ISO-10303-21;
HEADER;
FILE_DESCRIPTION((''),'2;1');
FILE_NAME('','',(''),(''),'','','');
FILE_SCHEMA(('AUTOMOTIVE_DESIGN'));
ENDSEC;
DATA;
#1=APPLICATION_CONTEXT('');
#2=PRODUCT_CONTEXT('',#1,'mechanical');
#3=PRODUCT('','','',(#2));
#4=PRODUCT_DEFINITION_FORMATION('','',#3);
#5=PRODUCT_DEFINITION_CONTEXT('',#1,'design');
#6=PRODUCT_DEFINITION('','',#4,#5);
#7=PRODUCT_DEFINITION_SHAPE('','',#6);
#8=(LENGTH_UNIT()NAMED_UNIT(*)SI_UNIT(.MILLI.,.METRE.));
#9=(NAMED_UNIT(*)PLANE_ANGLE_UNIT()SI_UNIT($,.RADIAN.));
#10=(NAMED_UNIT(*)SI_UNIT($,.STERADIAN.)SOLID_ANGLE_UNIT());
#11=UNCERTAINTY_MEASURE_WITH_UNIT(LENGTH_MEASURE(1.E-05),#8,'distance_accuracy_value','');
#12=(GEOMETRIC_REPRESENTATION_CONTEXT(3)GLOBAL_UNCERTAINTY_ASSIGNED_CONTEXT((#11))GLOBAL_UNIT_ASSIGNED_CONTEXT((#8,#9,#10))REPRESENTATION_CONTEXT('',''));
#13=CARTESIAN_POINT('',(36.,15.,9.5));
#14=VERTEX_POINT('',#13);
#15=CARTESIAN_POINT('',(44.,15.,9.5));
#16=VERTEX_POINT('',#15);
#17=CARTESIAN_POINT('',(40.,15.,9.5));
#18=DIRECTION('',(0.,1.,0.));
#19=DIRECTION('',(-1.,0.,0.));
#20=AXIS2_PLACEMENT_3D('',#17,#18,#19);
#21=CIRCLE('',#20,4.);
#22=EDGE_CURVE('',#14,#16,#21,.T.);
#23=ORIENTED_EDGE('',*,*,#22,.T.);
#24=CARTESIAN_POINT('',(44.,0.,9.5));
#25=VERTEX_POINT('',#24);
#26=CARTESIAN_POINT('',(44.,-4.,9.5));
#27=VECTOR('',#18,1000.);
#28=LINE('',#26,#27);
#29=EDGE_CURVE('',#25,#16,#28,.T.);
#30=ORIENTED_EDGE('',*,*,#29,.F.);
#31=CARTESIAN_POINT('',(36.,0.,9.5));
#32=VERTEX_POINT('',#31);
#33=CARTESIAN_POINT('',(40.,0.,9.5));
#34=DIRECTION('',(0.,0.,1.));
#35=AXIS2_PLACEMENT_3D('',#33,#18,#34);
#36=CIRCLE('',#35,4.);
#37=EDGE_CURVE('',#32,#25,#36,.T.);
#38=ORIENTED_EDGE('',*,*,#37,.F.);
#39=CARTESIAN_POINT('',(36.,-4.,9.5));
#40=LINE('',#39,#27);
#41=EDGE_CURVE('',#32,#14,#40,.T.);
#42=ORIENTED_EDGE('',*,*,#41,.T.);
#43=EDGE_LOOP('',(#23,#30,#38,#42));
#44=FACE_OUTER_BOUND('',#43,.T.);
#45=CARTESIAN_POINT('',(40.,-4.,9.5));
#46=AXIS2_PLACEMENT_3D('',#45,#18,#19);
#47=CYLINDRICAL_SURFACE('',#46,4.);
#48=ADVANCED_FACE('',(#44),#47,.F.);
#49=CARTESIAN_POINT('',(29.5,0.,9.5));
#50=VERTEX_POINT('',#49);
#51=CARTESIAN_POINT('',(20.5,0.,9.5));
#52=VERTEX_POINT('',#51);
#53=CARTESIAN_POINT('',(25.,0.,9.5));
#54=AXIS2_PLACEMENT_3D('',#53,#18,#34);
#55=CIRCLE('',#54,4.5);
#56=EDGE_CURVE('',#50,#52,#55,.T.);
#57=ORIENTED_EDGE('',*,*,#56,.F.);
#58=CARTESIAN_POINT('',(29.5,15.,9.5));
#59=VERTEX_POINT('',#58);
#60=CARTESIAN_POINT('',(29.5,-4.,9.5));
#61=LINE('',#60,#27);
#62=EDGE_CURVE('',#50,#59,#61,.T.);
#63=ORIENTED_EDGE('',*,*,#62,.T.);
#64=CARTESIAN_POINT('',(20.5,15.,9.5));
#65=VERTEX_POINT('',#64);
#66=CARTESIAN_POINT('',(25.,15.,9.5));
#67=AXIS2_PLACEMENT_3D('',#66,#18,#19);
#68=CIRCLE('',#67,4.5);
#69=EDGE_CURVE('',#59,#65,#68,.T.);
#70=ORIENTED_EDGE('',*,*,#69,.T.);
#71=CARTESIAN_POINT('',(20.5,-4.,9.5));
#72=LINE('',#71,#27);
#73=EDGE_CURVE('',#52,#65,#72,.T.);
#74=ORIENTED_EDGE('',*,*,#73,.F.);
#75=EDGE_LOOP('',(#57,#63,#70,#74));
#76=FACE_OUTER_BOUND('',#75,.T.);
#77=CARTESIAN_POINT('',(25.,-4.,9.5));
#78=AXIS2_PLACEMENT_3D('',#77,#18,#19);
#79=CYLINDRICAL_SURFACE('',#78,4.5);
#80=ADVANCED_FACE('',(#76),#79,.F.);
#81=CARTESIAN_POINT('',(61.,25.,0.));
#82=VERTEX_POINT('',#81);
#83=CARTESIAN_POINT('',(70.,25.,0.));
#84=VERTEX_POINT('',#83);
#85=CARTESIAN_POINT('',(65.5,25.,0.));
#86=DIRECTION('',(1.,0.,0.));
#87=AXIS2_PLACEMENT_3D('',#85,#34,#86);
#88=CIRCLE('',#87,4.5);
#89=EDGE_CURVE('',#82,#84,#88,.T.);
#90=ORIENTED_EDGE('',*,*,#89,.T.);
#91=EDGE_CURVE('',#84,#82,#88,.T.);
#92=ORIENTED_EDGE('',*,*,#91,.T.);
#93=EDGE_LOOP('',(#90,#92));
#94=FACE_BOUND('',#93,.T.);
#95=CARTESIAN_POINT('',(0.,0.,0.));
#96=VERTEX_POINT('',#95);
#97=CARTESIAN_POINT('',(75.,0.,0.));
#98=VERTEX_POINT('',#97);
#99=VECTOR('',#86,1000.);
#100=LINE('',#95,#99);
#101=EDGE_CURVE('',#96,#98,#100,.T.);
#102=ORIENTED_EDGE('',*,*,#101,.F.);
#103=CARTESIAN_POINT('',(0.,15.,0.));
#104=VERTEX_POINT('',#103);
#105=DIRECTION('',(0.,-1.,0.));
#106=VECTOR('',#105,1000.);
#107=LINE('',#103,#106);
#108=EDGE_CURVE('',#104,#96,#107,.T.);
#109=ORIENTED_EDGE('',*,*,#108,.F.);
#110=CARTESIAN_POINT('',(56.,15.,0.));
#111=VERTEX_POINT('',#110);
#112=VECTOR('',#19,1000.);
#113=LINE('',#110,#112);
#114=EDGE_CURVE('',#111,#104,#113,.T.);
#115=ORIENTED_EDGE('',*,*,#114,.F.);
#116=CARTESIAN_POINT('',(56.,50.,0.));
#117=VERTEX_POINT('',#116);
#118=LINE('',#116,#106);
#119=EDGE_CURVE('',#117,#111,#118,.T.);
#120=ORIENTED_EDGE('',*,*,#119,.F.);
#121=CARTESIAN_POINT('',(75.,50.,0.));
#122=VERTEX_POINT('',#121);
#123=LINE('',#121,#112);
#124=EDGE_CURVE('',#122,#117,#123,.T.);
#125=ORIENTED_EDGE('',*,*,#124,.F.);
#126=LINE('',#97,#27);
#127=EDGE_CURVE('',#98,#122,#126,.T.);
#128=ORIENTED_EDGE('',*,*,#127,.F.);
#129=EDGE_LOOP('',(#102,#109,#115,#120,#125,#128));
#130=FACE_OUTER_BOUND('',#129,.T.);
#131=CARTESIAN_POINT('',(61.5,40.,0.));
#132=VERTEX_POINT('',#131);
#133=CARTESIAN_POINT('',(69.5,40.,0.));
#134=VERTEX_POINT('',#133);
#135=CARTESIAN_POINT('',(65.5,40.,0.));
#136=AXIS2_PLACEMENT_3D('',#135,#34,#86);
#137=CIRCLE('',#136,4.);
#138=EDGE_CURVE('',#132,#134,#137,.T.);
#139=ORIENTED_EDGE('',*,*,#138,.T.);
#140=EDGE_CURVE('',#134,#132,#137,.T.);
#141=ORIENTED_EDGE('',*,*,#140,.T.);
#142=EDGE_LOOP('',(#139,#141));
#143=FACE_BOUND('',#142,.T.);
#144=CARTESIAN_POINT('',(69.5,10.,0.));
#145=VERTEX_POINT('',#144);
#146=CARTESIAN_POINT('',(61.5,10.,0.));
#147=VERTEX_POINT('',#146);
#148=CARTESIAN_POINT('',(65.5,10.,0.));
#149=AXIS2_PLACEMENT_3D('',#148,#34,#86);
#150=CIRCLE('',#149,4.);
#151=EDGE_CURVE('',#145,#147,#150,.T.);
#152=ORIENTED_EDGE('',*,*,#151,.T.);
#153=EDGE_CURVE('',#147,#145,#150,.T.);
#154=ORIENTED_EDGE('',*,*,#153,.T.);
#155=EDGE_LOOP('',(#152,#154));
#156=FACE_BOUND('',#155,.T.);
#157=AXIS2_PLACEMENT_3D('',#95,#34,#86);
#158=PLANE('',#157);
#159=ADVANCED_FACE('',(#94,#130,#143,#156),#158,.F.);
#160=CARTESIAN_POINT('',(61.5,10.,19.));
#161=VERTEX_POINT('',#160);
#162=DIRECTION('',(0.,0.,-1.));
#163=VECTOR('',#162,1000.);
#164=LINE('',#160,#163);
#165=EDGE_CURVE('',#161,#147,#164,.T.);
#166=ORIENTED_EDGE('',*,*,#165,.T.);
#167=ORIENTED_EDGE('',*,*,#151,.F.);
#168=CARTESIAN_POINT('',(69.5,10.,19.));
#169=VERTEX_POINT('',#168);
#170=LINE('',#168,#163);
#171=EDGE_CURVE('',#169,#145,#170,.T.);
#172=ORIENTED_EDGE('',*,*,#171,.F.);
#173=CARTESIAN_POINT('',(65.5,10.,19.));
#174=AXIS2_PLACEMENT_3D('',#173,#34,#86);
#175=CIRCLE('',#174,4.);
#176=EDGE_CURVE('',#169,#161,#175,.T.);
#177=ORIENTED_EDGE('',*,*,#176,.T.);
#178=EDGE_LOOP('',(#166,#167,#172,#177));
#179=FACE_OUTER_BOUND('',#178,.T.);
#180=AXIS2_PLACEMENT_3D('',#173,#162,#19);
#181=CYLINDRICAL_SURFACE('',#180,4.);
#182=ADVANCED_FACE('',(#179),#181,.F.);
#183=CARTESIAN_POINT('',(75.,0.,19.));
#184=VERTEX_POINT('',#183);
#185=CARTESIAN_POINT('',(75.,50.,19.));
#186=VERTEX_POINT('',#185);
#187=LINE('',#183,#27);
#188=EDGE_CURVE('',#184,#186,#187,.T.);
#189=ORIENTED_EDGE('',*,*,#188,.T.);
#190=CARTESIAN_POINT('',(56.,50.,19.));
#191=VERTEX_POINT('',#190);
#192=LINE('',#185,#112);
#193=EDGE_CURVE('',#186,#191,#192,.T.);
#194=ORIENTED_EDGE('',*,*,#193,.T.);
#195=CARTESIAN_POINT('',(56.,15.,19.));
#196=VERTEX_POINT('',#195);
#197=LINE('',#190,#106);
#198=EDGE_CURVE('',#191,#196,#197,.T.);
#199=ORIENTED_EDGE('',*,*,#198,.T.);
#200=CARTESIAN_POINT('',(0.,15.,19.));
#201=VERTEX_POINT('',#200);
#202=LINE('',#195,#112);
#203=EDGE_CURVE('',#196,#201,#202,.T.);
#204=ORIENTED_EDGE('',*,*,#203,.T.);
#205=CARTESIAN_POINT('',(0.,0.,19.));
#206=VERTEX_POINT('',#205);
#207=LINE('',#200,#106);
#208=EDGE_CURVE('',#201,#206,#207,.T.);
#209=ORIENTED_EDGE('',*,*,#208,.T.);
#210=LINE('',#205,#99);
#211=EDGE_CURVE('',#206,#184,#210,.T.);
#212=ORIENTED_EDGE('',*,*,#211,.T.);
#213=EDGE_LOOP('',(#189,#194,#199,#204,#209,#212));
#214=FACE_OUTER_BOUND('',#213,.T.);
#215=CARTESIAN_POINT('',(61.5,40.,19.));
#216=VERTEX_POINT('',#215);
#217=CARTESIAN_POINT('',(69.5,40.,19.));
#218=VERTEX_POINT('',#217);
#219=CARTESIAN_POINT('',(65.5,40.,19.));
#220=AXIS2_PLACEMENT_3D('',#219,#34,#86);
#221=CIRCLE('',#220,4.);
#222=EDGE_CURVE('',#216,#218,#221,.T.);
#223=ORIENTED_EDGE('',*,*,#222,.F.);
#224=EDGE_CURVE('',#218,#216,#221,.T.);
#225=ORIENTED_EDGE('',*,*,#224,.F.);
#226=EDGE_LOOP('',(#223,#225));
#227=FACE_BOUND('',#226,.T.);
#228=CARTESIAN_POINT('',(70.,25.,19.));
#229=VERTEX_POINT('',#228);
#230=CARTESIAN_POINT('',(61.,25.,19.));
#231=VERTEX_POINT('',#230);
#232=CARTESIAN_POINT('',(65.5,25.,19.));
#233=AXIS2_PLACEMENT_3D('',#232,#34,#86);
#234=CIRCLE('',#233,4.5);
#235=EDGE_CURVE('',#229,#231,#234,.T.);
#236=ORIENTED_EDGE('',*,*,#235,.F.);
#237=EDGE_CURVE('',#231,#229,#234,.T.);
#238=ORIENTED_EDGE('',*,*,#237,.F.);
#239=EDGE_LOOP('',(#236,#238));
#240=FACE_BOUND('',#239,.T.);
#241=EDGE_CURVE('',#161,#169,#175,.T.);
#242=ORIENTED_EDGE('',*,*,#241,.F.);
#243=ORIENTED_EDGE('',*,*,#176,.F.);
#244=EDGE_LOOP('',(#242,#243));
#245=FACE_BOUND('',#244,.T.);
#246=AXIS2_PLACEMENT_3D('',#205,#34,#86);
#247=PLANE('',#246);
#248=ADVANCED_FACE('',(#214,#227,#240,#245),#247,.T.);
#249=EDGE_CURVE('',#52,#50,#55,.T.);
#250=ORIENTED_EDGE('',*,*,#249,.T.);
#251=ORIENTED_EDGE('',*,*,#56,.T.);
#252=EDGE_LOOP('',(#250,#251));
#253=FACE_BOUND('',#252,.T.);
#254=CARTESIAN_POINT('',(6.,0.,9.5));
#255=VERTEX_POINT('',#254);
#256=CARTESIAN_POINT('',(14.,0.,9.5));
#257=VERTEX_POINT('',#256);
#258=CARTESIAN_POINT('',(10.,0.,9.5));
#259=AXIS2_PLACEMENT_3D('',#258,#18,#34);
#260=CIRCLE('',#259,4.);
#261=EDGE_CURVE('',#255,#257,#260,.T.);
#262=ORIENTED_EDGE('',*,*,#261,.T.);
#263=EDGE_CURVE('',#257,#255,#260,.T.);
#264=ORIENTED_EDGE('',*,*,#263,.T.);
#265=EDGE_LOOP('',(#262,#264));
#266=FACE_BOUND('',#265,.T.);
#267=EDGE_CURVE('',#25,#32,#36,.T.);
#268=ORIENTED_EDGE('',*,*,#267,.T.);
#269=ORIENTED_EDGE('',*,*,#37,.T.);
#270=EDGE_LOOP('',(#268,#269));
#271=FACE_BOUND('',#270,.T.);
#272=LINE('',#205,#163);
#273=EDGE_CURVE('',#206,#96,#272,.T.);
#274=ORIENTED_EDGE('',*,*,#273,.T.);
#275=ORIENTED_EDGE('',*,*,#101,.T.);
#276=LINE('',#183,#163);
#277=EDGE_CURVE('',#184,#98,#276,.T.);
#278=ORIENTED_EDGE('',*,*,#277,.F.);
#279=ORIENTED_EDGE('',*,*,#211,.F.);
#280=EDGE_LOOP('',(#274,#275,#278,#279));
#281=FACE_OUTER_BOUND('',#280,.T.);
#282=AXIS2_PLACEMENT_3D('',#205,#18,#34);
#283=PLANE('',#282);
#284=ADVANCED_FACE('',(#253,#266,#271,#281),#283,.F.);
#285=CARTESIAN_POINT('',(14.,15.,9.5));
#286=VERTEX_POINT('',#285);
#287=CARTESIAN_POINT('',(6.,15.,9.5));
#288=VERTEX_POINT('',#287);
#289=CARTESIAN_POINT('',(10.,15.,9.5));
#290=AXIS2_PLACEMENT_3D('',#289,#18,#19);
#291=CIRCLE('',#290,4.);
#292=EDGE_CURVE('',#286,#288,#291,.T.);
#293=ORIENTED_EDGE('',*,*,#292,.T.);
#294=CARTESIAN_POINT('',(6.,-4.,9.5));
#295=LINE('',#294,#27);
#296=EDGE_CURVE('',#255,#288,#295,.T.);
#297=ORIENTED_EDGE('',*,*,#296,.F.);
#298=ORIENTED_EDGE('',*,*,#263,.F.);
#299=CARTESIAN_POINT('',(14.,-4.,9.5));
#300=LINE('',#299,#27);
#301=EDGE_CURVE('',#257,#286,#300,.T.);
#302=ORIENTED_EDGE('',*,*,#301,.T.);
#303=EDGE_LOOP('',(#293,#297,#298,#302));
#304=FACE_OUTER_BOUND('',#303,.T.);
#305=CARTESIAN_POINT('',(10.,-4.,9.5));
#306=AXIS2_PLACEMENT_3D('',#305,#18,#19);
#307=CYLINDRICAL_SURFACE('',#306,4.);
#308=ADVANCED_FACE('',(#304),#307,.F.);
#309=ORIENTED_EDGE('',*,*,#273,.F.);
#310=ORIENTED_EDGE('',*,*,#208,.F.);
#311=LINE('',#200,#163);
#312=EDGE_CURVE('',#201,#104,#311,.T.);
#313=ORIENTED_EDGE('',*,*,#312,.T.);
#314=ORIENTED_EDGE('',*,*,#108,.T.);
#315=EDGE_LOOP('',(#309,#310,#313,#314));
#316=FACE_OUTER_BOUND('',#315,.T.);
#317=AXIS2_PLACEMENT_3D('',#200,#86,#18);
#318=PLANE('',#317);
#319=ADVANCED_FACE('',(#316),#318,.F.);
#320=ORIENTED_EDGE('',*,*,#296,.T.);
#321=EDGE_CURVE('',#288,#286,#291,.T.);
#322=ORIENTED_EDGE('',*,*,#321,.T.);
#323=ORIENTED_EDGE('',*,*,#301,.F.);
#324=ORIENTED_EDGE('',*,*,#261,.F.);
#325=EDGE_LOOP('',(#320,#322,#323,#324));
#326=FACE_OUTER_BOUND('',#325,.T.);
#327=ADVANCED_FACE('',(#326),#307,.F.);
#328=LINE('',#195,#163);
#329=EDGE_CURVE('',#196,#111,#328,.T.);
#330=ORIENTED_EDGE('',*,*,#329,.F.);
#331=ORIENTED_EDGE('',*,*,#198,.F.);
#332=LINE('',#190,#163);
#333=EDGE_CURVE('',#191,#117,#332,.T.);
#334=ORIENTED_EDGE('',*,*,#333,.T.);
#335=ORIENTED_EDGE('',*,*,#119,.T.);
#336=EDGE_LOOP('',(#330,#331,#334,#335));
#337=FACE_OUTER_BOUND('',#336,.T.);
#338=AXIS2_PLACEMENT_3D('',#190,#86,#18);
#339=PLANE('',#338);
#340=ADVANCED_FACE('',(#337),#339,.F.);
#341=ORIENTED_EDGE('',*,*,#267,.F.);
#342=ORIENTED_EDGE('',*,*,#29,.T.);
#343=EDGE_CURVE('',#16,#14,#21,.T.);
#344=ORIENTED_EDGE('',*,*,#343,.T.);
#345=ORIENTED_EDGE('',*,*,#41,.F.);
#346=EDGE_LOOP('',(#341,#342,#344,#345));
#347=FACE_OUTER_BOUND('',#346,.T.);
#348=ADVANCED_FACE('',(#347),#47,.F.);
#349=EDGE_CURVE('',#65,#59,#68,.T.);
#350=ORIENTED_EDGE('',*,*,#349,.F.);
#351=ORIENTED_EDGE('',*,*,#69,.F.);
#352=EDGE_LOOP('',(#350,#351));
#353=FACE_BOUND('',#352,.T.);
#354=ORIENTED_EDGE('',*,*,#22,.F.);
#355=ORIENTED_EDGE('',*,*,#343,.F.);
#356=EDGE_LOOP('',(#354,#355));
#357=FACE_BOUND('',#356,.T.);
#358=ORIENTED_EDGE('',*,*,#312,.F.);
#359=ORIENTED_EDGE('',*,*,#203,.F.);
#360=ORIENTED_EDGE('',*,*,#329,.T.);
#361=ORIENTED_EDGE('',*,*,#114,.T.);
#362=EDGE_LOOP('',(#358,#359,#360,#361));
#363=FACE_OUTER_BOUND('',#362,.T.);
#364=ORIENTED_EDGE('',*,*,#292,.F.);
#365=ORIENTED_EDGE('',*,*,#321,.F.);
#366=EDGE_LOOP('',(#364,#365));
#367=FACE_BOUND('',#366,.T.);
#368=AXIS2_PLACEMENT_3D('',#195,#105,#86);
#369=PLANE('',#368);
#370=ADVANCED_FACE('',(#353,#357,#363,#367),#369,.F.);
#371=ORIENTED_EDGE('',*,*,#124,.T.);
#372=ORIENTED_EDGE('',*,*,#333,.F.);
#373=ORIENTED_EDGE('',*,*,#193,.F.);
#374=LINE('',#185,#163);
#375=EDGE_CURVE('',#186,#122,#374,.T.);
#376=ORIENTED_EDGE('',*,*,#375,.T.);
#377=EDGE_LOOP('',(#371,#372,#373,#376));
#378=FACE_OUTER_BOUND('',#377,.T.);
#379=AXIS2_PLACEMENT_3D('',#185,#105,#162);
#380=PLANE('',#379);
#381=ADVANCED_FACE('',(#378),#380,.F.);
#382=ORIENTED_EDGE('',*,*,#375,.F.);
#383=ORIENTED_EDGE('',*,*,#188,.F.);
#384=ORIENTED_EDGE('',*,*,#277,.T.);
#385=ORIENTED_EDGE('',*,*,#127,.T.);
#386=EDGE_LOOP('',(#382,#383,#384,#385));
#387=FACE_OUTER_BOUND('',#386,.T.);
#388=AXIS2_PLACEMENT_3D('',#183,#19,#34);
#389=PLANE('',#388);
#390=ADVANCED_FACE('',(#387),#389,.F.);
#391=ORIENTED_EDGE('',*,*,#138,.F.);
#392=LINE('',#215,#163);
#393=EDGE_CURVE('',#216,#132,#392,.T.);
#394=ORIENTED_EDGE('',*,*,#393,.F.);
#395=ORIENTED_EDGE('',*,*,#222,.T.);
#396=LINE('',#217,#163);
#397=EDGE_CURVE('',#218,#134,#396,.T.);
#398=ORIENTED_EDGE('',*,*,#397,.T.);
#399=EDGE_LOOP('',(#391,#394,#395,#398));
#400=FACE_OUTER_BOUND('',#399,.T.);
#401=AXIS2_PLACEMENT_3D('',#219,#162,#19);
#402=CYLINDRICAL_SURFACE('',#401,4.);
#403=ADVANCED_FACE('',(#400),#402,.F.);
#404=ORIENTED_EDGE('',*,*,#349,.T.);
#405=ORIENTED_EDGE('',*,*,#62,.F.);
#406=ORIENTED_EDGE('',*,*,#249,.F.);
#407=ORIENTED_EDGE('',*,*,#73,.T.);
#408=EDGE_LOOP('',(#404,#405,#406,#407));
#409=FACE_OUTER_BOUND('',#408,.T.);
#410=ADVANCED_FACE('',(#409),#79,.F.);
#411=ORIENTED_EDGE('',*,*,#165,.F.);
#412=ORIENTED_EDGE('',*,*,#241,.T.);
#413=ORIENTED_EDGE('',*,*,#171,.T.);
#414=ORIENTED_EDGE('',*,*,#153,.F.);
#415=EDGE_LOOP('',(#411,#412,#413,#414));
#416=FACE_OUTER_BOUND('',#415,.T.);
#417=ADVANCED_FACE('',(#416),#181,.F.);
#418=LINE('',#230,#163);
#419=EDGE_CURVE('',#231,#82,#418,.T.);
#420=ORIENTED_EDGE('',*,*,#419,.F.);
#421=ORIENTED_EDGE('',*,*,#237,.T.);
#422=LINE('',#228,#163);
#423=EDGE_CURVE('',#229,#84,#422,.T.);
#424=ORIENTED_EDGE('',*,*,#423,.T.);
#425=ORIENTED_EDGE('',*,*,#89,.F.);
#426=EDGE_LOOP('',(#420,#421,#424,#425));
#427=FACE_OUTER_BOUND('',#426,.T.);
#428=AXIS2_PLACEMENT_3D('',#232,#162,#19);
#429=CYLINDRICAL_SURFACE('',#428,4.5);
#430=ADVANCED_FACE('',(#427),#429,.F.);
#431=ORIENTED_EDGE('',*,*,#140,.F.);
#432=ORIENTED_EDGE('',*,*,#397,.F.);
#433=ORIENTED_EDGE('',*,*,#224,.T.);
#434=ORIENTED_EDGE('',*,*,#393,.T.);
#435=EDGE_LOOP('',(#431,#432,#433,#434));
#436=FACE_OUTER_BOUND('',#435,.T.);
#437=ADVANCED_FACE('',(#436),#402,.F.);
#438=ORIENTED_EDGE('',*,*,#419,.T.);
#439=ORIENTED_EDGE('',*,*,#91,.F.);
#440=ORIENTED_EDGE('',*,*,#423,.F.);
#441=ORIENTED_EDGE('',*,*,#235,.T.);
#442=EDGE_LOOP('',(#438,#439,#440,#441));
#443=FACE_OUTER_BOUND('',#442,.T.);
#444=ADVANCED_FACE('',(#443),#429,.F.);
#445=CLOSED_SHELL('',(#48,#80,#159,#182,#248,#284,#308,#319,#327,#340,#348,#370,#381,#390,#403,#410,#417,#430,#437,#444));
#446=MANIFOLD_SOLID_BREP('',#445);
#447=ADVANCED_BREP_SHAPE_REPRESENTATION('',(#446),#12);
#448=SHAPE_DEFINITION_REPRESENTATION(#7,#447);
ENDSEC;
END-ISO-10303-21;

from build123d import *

# Parameters (mm, degrees)
SKETCH1_R           = 4
SKETCH1_R_2         = 4.5
BOSS_EXTRUDE1_DEPTH = 19
SKETCH2_R           = 4
SKETCH2_R_2         = 4.5
CUT_EXTRUDE1_DEPTH  = 19


with BuildPart() as part:
    # Sketch1 → Boss-Extrude1 (new body)
    with BuildSketch(Plane.XY):
        Polygon((0, 0), (75, 0), (75, 50), (56, 50), (56, 15), (0, 15), align=None)
        with Locations((65.5, 10)):
            Circle(SKETCH1_R, mode=Mode.SUBTRACT)
        with Locations((65.5, 25)):
            Circle(SKETCH1_R_2, mode=Mode.SUBTRACT)
        with Locations((65.5, 40)):
            Circle(SKETCH1_R, mode=Mode.SUBTRACT)
    extrude(amount=BOSS_EXTRUDE1_DEPTH)

    # Sketch2 → Cut-Extrude1 (cut)
    with BuildSketch(Plane(origin=(0, 15, 0), x_dir=(1, 0, 0), z_dir=(0, 1, 0))):
        with Locations(Location((10, -9.5, 0), (0, 0, 180))):
            Circle(SKETCH2_R)
        with Locations(Location((25, -9.5, 0), (0, 0, 180))):
            Circle(SKETCH2_R_2)
        with Locations(Location((40, -9.5, 0), (0, 0, 180))):
            Circle(SKETCH2_R)
    extrude(amount=-CUT_EXTRUDE1_DEPTH, mode=Mode.SUBTRACT)


solid = part.part
